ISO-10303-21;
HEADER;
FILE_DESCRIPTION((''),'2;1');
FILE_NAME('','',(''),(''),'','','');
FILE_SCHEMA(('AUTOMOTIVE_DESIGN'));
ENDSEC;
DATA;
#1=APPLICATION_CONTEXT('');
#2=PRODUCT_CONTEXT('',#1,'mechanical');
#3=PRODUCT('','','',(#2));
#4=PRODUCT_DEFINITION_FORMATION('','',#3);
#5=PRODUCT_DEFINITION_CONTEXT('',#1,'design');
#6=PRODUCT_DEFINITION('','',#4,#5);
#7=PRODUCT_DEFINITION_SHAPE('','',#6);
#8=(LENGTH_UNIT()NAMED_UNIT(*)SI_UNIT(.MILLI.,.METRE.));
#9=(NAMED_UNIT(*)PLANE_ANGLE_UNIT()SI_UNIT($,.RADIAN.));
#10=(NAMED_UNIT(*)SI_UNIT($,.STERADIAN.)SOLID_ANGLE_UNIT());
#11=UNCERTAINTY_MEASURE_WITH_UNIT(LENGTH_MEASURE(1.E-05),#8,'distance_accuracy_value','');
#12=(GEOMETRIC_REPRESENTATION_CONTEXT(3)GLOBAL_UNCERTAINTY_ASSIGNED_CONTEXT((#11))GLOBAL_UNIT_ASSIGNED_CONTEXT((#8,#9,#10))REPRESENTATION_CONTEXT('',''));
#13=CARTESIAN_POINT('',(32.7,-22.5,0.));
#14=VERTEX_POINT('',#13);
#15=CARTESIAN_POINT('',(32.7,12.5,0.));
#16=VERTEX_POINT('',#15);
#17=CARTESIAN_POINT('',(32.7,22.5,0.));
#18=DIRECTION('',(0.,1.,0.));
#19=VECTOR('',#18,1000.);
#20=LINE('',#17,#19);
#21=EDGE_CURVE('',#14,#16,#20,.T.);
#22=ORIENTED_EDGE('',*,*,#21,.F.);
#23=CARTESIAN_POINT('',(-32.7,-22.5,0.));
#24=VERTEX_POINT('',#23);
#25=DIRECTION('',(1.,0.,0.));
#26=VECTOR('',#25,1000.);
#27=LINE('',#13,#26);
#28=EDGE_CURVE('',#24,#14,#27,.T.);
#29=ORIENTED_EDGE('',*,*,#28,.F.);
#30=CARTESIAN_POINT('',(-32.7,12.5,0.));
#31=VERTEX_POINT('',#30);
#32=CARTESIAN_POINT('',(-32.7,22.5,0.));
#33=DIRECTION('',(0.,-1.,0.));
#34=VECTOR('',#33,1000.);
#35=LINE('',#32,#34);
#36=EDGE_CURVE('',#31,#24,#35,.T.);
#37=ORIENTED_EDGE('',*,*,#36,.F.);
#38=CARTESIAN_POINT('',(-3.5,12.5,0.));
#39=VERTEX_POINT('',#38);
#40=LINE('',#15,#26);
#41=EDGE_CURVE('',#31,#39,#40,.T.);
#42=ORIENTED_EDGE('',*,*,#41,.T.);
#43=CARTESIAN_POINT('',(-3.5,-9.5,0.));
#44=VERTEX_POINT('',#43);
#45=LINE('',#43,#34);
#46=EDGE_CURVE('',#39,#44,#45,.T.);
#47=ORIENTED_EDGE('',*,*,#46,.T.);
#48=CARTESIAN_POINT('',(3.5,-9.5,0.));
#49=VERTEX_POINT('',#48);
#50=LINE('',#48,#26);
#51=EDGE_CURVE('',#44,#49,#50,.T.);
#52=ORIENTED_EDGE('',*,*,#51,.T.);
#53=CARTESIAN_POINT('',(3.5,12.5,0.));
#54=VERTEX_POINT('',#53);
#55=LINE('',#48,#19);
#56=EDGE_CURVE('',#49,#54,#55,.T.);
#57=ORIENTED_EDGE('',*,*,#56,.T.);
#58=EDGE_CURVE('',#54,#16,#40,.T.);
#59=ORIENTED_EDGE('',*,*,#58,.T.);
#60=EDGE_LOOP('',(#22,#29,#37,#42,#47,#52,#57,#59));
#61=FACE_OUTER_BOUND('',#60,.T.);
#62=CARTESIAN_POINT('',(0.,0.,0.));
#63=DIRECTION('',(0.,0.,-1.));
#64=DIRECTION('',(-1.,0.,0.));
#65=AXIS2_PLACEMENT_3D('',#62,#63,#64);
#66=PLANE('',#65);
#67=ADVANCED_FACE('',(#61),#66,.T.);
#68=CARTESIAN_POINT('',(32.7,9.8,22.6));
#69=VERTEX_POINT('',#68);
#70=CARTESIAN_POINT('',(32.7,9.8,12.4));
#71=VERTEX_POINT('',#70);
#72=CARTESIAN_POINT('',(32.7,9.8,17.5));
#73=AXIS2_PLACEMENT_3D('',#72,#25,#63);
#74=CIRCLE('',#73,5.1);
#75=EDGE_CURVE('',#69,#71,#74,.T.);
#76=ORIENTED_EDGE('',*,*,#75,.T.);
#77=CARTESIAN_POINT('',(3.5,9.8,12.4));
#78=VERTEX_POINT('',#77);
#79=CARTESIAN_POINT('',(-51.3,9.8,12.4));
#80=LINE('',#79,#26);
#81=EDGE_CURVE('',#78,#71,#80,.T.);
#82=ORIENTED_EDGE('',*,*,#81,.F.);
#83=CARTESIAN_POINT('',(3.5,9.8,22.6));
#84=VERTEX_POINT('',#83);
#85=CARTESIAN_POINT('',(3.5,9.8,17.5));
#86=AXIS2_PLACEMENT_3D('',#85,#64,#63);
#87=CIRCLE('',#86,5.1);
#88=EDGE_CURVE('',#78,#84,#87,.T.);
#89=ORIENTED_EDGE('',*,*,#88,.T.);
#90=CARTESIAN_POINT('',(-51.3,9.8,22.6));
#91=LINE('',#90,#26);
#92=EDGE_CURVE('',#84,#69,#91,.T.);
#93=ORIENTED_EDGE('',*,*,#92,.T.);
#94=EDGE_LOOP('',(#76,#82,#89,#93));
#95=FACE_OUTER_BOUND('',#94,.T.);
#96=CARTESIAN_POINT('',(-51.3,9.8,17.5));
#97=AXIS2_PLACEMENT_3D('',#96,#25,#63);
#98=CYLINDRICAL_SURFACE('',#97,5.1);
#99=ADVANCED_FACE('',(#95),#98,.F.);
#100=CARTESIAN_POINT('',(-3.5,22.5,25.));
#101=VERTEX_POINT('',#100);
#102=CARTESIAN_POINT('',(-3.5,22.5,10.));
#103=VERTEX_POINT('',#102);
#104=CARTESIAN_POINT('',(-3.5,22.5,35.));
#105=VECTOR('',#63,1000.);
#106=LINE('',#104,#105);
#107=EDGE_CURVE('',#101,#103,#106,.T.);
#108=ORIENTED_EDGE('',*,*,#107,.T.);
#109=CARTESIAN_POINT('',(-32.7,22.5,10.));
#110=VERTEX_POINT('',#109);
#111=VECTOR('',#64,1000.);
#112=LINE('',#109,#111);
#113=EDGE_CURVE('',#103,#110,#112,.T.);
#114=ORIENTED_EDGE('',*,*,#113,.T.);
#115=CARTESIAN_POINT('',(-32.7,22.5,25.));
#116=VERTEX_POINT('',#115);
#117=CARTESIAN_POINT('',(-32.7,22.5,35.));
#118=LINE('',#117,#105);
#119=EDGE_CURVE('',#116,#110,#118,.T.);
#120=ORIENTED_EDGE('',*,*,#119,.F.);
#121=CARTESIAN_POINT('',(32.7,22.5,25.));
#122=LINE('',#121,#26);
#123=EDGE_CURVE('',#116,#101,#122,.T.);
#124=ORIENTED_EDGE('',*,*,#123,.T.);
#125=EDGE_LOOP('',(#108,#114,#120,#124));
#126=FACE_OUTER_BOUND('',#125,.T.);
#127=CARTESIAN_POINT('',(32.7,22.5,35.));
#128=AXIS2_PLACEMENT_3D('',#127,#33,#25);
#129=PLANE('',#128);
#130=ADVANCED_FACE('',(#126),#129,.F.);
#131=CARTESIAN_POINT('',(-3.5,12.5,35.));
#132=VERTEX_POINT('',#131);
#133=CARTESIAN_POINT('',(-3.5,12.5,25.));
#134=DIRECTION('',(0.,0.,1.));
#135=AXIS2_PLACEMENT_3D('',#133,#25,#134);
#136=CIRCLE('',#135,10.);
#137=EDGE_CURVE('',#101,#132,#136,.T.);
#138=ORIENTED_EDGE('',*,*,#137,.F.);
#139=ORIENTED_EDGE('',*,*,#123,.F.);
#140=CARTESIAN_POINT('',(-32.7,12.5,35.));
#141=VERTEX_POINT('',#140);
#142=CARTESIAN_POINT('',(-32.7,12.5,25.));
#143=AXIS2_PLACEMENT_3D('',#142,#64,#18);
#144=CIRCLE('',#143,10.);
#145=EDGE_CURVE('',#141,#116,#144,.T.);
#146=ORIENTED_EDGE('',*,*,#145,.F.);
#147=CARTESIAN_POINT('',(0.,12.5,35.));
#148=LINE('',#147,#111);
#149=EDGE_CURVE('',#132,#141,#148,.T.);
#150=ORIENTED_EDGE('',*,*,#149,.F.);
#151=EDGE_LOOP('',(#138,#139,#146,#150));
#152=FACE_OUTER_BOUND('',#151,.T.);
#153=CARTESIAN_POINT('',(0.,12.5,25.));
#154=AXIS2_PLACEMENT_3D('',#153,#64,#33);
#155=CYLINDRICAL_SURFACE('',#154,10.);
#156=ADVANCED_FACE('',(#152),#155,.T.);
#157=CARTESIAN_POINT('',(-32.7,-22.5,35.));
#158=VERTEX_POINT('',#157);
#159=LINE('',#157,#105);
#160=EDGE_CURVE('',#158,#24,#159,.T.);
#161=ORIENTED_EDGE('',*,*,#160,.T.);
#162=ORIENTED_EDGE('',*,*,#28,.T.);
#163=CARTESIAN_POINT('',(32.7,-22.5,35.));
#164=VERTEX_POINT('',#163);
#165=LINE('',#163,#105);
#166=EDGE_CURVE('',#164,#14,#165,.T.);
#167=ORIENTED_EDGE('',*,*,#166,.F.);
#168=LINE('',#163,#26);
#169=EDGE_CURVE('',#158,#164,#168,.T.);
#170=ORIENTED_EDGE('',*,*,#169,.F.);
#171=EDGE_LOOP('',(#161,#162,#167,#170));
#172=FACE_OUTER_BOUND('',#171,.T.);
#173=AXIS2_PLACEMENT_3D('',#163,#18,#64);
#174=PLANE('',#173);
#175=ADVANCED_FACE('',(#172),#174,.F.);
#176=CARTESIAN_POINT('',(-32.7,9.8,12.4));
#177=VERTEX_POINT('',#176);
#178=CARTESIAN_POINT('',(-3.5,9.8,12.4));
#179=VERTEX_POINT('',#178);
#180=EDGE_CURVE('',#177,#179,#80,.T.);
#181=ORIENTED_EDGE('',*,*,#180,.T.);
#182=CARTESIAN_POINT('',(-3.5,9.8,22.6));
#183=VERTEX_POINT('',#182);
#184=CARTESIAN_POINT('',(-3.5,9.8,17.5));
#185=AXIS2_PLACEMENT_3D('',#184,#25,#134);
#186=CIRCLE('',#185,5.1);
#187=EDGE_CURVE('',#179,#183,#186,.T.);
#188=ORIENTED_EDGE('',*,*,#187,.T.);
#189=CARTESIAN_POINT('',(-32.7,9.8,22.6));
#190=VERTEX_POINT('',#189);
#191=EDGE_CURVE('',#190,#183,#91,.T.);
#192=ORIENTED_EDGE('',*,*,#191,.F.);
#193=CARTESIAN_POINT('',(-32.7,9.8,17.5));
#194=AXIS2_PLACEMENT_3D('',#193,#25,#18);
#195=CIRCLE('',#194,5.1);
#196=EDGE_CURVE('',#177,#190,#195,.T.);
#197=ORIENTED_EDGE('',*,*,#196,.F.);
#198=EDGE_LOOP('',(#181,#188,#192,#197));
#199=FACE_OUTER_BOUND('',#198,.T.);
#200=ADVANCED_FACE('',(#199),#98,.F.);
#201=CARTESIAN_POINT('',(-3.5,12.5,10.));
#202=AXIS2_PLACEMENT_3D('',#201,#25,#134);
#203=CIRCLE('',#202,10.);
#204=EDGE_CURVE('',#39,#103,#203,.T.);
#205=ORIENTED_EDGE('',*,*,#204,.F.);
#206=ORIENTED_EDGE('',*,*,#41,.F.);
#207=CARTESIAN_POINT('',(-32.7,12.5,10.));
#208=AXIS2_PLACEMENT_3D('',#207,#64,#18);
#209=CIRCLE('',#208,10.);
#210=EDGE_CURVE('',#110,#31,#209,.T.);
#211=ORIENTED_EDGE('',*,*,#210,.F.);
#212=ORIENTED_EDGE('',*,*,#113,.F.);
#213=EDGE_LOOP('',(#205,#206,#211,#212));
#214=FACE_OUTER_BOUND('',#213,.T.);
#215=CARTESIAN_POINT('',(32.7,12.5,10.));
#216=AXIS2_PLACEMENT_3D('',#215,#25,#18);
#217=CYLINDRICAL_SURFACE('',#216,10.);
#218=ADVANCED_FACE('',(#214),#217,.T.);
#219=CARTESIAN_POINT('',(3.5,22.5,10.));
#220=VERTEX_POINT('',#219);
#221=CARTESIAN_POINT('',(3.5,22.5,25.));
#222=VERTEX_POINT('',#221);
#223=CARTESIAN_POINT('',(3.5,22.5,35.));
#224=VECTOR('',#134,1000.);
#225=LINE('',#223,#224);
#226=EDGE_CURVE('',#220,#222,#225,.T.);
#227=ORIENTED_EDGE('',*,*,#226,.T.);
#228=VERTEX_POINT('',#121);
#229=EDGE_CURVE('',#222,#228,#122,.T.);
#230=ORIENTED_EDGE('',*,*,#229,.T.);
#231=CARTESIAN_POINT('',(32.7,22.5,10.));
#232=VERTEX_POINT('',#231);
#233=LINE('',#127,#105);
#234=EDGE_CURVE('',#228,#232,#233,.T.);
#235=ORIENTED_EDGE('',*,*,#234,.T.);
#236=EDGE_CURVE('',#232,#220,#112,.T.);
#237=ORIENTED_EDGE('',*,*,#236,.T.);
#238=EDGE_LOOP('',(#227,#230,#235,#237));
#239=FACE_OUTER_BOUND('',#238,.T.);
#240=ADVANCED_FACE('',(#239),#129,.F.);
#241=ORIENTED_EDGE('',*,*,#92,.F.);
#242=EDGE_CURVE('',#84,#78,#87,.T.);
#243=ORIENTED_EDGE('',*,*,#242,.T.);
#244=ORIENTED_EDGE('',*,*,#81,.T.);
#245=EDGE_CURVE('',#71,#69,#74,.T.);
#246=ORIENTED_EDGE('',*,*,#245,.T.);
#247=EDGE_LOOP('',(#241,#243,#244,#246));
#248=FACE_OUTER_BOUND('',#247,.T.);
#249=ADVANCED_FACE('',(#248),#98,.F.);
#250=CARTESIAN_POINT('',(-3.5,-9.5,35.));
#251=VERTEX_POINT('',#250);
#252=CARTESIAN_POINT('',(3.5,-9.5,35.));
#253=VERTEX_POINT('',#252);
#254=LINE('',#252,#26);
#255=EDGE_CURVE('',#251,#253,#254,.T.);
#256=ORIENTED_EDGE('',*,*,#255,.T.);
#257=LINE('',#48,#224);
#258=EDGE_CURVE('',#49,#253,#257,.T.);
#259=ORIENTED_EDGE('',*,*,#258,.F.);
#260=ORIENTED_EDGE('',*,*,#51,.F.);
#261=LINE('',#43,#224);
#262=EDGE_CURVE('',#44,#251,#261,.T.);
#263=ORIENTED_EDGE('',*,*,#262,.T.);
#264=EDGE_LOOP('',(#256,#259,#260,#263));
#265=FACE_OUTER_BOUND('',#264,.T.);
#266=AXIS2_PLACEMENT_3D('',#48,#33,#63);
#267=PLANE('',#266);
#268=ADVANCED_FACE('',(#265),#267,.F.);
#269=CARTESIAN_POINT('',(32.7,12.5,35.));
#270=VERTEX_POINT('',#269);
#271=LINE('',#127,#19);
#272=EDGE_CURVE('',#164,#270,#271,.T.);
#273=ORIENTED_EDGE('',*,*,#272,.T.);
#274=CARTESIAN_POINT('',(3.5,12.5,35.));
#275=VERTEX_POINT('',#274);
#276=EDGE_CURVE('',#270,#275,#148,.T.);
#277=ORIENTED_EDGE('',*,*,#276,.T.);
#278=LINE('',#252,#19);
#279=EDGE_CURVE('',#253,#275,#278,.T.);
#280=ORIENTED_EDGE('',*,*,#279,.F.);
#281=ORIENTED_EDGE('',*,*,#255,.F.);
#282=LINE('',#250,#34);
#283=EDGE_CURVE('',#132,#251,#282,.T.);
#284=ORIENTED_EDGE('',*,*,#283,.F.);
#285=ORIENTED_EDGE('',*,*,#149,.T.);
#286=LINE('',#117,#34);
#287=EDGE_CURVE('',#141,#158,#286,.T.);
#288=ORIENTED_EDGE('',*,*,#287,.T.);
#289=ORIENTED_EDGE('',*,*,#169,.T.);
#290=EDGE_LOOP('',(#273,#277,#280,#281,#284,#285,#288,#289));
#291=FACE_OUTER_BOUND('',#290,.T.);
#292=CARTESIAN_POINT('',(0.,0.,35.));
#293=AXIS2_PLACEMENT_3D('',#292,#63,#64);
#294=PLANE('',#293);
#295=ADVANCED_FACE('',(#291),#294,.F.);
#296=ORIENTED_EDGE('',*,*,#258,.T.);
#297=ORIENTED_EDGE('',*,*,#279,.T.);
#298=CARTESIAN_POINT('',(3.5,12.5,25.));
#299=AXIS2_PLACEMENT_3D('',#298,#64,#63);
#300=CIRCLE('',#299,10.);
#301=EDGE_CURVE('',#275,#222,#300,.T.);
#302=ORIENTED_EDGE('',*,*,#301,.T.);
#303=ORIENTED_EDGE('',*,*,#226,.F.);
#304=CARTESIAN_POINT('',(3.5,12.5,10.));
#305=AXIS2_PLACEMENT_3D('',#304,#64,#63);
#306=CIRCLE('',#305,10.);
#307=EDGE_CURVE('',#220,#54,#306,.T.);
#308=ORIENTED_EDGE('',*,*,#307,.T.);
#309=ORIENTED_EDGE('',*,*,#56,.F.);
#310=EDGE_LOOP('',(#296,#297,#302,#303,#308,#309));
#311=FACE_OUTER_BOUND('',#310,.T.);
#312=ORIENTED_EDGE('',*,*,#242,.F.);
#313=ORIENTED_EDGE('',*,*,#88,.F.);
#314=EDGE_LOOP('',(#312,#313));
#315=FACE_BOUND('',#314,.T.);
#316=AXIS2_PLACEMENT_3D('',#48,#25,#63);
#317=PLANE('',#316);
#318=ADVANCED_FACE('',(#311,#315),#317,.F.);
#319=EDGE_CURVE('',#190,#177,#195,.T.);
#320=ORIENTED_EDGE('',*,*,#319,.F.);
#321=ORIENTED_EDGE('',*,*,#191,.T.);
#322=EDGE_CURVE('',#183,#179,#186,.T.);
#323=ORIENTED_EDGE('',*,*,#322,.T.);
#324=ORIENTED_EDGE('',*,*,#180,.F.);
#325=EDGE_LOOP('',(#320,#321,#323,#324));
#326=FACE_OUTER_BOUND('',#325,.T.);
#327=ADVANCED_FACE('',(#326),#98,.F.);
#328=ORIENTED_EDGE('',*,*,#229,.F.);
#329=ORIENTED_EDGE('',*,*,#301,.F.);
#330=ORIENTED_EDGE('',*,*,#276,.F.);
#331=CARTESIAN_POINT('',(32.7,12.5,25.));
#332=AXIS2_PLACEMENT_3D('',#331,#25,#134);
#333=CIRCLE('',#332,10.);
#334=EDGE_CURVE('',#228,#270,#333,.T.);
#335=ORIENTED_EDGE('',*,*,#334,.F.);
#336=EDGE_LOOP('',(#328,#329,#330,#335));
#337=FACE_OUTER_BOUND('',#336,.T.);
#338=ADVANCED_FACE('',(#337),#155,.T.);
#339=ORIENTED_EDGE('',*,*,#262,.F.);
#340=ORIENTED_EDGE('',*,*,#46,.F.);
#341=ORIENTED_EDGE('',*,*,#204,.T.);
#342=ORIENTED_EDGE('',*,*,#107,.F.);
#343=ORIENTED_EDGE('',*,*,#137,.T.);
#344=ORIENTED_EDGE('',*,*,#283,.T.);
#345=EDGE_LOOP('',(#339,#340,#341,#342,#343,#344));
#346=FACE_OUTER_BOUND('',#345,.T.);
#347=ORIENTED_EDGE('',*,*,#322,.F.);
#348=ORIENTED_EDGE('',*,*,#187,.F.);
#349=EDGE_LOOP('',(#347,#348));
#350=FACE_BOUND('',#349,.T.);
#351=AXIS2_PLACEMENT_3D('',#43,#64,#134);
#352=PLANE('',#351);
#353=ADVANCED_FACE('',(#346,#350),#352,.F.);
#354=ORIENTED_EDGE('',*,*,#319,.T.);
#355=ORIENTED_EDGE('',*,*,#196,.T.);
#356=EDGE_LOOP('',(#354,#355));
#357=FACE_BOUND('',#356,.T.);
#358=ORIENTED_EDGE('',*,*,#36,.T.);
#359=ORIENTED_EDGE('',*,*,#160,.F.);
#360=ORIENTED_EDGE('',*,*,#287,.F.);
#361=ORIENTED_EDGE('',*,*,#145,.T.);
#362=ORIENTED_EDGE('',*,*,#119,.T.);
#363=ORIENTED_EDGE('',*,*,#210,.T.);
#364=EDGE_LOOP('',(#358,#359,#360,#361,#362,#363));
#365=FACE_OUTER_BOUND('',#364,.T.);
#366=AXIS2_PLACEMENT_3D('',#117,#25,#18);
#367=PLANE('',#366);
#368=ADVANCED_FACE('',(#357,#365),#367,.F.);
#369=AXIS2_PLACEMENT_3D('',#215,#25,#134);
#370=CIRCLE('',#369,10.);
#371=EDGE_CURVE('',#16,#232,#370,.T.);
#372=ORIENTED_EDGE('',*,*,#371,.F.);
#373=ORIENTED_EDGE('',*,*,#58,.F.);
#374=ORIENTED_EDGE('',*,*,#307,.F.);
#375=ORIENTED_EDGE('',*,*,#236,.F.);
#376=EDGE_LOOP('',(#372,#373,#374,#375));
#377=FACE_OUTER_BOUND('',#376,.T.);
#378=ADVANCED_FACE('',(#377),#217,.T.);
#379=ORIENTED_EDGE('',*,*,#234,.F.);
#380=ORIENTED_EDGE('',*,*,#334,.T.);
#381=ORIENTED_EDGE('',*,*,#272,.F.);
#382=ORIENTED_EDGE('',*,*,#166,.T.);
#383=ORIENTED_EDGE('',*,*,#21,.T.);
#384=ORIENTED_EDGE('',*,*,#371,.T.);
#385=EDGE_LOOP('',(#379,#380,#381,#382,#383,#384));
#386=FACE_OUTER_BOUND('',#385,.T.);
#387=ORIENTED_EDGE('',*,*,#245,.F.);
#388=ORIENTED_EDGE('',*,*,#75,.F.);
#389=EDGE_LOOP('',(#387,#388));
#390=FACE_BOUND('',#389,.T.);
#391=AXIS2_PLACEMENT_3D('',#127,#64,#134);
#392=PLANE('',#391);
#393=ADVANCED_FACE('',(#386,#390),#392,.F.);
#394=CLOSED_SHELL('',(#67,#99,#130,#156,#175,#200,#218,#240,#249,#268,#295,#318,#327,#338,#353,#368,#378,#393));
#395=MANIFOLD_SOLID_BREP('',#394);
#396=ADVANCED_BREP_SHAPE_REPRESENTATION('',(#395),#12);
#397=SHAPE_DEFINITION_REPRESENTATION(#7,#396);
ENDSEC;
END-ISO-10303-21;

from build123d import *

# Parameters (mm, degrees)
SKETCH_1_W          = 65.4
SKETCH_1_H          = 45
EXTRUDE_1_DEPTH     = 35
FILLET_1_R          = 10
SKETCH_2_R          = 5.1
CUT_EXTRUDE_1_DEPTH = 84
SKETCH_3_W          = 7
SKETCH_3_H          = 50
CUT_EXTRUDE_2_DEPTH = 35


with BuildPart() as part:
    # 草图1 → 凸台-拉伸1 (new body)
    with BuildSketch(Plane.XY):
        Rectangle(SKETCH_1_W, SKETCH_1_H)
    extrude(amount=EXTRUDE_1_DEPTH)

    # 圆角1
    fillet_1_edges = [part.edges().sort_by_distance(p)[0] for p in [
        (0, 22.5, 35),
        (0, 22.5, 0),
    ]]
    fillet(fillet_1_edges, radius=FILLET_1_R)

    # 草图2 → 切除-拉伸1 (cut)
    with BuildSketch(Plane(origin=(32.7, 0, 0), x_dir=(0, 0, -1), z_dir=(1, 0, 0))):
        with Locations((-17.5, 9.8)):
            Circle(SKETCH_2_R)
    extrude(amount=-CUT_EXTRUDE_1_DEPTH, mode=Mode.SUBTRACT)

    # 草图3 → 切除-拉伸2 (cut)
    with BuildSketch(Plane.XY.offset(35)):
        with Locations((0, 15.5)):
            Rectangle(SKETCH_3_W, SKETCH_3_H)
    extrude(amount=-CUT_EXTRUDE_2_DEPTH, mode=Mode.SUBTRACT)


solid = part.part
